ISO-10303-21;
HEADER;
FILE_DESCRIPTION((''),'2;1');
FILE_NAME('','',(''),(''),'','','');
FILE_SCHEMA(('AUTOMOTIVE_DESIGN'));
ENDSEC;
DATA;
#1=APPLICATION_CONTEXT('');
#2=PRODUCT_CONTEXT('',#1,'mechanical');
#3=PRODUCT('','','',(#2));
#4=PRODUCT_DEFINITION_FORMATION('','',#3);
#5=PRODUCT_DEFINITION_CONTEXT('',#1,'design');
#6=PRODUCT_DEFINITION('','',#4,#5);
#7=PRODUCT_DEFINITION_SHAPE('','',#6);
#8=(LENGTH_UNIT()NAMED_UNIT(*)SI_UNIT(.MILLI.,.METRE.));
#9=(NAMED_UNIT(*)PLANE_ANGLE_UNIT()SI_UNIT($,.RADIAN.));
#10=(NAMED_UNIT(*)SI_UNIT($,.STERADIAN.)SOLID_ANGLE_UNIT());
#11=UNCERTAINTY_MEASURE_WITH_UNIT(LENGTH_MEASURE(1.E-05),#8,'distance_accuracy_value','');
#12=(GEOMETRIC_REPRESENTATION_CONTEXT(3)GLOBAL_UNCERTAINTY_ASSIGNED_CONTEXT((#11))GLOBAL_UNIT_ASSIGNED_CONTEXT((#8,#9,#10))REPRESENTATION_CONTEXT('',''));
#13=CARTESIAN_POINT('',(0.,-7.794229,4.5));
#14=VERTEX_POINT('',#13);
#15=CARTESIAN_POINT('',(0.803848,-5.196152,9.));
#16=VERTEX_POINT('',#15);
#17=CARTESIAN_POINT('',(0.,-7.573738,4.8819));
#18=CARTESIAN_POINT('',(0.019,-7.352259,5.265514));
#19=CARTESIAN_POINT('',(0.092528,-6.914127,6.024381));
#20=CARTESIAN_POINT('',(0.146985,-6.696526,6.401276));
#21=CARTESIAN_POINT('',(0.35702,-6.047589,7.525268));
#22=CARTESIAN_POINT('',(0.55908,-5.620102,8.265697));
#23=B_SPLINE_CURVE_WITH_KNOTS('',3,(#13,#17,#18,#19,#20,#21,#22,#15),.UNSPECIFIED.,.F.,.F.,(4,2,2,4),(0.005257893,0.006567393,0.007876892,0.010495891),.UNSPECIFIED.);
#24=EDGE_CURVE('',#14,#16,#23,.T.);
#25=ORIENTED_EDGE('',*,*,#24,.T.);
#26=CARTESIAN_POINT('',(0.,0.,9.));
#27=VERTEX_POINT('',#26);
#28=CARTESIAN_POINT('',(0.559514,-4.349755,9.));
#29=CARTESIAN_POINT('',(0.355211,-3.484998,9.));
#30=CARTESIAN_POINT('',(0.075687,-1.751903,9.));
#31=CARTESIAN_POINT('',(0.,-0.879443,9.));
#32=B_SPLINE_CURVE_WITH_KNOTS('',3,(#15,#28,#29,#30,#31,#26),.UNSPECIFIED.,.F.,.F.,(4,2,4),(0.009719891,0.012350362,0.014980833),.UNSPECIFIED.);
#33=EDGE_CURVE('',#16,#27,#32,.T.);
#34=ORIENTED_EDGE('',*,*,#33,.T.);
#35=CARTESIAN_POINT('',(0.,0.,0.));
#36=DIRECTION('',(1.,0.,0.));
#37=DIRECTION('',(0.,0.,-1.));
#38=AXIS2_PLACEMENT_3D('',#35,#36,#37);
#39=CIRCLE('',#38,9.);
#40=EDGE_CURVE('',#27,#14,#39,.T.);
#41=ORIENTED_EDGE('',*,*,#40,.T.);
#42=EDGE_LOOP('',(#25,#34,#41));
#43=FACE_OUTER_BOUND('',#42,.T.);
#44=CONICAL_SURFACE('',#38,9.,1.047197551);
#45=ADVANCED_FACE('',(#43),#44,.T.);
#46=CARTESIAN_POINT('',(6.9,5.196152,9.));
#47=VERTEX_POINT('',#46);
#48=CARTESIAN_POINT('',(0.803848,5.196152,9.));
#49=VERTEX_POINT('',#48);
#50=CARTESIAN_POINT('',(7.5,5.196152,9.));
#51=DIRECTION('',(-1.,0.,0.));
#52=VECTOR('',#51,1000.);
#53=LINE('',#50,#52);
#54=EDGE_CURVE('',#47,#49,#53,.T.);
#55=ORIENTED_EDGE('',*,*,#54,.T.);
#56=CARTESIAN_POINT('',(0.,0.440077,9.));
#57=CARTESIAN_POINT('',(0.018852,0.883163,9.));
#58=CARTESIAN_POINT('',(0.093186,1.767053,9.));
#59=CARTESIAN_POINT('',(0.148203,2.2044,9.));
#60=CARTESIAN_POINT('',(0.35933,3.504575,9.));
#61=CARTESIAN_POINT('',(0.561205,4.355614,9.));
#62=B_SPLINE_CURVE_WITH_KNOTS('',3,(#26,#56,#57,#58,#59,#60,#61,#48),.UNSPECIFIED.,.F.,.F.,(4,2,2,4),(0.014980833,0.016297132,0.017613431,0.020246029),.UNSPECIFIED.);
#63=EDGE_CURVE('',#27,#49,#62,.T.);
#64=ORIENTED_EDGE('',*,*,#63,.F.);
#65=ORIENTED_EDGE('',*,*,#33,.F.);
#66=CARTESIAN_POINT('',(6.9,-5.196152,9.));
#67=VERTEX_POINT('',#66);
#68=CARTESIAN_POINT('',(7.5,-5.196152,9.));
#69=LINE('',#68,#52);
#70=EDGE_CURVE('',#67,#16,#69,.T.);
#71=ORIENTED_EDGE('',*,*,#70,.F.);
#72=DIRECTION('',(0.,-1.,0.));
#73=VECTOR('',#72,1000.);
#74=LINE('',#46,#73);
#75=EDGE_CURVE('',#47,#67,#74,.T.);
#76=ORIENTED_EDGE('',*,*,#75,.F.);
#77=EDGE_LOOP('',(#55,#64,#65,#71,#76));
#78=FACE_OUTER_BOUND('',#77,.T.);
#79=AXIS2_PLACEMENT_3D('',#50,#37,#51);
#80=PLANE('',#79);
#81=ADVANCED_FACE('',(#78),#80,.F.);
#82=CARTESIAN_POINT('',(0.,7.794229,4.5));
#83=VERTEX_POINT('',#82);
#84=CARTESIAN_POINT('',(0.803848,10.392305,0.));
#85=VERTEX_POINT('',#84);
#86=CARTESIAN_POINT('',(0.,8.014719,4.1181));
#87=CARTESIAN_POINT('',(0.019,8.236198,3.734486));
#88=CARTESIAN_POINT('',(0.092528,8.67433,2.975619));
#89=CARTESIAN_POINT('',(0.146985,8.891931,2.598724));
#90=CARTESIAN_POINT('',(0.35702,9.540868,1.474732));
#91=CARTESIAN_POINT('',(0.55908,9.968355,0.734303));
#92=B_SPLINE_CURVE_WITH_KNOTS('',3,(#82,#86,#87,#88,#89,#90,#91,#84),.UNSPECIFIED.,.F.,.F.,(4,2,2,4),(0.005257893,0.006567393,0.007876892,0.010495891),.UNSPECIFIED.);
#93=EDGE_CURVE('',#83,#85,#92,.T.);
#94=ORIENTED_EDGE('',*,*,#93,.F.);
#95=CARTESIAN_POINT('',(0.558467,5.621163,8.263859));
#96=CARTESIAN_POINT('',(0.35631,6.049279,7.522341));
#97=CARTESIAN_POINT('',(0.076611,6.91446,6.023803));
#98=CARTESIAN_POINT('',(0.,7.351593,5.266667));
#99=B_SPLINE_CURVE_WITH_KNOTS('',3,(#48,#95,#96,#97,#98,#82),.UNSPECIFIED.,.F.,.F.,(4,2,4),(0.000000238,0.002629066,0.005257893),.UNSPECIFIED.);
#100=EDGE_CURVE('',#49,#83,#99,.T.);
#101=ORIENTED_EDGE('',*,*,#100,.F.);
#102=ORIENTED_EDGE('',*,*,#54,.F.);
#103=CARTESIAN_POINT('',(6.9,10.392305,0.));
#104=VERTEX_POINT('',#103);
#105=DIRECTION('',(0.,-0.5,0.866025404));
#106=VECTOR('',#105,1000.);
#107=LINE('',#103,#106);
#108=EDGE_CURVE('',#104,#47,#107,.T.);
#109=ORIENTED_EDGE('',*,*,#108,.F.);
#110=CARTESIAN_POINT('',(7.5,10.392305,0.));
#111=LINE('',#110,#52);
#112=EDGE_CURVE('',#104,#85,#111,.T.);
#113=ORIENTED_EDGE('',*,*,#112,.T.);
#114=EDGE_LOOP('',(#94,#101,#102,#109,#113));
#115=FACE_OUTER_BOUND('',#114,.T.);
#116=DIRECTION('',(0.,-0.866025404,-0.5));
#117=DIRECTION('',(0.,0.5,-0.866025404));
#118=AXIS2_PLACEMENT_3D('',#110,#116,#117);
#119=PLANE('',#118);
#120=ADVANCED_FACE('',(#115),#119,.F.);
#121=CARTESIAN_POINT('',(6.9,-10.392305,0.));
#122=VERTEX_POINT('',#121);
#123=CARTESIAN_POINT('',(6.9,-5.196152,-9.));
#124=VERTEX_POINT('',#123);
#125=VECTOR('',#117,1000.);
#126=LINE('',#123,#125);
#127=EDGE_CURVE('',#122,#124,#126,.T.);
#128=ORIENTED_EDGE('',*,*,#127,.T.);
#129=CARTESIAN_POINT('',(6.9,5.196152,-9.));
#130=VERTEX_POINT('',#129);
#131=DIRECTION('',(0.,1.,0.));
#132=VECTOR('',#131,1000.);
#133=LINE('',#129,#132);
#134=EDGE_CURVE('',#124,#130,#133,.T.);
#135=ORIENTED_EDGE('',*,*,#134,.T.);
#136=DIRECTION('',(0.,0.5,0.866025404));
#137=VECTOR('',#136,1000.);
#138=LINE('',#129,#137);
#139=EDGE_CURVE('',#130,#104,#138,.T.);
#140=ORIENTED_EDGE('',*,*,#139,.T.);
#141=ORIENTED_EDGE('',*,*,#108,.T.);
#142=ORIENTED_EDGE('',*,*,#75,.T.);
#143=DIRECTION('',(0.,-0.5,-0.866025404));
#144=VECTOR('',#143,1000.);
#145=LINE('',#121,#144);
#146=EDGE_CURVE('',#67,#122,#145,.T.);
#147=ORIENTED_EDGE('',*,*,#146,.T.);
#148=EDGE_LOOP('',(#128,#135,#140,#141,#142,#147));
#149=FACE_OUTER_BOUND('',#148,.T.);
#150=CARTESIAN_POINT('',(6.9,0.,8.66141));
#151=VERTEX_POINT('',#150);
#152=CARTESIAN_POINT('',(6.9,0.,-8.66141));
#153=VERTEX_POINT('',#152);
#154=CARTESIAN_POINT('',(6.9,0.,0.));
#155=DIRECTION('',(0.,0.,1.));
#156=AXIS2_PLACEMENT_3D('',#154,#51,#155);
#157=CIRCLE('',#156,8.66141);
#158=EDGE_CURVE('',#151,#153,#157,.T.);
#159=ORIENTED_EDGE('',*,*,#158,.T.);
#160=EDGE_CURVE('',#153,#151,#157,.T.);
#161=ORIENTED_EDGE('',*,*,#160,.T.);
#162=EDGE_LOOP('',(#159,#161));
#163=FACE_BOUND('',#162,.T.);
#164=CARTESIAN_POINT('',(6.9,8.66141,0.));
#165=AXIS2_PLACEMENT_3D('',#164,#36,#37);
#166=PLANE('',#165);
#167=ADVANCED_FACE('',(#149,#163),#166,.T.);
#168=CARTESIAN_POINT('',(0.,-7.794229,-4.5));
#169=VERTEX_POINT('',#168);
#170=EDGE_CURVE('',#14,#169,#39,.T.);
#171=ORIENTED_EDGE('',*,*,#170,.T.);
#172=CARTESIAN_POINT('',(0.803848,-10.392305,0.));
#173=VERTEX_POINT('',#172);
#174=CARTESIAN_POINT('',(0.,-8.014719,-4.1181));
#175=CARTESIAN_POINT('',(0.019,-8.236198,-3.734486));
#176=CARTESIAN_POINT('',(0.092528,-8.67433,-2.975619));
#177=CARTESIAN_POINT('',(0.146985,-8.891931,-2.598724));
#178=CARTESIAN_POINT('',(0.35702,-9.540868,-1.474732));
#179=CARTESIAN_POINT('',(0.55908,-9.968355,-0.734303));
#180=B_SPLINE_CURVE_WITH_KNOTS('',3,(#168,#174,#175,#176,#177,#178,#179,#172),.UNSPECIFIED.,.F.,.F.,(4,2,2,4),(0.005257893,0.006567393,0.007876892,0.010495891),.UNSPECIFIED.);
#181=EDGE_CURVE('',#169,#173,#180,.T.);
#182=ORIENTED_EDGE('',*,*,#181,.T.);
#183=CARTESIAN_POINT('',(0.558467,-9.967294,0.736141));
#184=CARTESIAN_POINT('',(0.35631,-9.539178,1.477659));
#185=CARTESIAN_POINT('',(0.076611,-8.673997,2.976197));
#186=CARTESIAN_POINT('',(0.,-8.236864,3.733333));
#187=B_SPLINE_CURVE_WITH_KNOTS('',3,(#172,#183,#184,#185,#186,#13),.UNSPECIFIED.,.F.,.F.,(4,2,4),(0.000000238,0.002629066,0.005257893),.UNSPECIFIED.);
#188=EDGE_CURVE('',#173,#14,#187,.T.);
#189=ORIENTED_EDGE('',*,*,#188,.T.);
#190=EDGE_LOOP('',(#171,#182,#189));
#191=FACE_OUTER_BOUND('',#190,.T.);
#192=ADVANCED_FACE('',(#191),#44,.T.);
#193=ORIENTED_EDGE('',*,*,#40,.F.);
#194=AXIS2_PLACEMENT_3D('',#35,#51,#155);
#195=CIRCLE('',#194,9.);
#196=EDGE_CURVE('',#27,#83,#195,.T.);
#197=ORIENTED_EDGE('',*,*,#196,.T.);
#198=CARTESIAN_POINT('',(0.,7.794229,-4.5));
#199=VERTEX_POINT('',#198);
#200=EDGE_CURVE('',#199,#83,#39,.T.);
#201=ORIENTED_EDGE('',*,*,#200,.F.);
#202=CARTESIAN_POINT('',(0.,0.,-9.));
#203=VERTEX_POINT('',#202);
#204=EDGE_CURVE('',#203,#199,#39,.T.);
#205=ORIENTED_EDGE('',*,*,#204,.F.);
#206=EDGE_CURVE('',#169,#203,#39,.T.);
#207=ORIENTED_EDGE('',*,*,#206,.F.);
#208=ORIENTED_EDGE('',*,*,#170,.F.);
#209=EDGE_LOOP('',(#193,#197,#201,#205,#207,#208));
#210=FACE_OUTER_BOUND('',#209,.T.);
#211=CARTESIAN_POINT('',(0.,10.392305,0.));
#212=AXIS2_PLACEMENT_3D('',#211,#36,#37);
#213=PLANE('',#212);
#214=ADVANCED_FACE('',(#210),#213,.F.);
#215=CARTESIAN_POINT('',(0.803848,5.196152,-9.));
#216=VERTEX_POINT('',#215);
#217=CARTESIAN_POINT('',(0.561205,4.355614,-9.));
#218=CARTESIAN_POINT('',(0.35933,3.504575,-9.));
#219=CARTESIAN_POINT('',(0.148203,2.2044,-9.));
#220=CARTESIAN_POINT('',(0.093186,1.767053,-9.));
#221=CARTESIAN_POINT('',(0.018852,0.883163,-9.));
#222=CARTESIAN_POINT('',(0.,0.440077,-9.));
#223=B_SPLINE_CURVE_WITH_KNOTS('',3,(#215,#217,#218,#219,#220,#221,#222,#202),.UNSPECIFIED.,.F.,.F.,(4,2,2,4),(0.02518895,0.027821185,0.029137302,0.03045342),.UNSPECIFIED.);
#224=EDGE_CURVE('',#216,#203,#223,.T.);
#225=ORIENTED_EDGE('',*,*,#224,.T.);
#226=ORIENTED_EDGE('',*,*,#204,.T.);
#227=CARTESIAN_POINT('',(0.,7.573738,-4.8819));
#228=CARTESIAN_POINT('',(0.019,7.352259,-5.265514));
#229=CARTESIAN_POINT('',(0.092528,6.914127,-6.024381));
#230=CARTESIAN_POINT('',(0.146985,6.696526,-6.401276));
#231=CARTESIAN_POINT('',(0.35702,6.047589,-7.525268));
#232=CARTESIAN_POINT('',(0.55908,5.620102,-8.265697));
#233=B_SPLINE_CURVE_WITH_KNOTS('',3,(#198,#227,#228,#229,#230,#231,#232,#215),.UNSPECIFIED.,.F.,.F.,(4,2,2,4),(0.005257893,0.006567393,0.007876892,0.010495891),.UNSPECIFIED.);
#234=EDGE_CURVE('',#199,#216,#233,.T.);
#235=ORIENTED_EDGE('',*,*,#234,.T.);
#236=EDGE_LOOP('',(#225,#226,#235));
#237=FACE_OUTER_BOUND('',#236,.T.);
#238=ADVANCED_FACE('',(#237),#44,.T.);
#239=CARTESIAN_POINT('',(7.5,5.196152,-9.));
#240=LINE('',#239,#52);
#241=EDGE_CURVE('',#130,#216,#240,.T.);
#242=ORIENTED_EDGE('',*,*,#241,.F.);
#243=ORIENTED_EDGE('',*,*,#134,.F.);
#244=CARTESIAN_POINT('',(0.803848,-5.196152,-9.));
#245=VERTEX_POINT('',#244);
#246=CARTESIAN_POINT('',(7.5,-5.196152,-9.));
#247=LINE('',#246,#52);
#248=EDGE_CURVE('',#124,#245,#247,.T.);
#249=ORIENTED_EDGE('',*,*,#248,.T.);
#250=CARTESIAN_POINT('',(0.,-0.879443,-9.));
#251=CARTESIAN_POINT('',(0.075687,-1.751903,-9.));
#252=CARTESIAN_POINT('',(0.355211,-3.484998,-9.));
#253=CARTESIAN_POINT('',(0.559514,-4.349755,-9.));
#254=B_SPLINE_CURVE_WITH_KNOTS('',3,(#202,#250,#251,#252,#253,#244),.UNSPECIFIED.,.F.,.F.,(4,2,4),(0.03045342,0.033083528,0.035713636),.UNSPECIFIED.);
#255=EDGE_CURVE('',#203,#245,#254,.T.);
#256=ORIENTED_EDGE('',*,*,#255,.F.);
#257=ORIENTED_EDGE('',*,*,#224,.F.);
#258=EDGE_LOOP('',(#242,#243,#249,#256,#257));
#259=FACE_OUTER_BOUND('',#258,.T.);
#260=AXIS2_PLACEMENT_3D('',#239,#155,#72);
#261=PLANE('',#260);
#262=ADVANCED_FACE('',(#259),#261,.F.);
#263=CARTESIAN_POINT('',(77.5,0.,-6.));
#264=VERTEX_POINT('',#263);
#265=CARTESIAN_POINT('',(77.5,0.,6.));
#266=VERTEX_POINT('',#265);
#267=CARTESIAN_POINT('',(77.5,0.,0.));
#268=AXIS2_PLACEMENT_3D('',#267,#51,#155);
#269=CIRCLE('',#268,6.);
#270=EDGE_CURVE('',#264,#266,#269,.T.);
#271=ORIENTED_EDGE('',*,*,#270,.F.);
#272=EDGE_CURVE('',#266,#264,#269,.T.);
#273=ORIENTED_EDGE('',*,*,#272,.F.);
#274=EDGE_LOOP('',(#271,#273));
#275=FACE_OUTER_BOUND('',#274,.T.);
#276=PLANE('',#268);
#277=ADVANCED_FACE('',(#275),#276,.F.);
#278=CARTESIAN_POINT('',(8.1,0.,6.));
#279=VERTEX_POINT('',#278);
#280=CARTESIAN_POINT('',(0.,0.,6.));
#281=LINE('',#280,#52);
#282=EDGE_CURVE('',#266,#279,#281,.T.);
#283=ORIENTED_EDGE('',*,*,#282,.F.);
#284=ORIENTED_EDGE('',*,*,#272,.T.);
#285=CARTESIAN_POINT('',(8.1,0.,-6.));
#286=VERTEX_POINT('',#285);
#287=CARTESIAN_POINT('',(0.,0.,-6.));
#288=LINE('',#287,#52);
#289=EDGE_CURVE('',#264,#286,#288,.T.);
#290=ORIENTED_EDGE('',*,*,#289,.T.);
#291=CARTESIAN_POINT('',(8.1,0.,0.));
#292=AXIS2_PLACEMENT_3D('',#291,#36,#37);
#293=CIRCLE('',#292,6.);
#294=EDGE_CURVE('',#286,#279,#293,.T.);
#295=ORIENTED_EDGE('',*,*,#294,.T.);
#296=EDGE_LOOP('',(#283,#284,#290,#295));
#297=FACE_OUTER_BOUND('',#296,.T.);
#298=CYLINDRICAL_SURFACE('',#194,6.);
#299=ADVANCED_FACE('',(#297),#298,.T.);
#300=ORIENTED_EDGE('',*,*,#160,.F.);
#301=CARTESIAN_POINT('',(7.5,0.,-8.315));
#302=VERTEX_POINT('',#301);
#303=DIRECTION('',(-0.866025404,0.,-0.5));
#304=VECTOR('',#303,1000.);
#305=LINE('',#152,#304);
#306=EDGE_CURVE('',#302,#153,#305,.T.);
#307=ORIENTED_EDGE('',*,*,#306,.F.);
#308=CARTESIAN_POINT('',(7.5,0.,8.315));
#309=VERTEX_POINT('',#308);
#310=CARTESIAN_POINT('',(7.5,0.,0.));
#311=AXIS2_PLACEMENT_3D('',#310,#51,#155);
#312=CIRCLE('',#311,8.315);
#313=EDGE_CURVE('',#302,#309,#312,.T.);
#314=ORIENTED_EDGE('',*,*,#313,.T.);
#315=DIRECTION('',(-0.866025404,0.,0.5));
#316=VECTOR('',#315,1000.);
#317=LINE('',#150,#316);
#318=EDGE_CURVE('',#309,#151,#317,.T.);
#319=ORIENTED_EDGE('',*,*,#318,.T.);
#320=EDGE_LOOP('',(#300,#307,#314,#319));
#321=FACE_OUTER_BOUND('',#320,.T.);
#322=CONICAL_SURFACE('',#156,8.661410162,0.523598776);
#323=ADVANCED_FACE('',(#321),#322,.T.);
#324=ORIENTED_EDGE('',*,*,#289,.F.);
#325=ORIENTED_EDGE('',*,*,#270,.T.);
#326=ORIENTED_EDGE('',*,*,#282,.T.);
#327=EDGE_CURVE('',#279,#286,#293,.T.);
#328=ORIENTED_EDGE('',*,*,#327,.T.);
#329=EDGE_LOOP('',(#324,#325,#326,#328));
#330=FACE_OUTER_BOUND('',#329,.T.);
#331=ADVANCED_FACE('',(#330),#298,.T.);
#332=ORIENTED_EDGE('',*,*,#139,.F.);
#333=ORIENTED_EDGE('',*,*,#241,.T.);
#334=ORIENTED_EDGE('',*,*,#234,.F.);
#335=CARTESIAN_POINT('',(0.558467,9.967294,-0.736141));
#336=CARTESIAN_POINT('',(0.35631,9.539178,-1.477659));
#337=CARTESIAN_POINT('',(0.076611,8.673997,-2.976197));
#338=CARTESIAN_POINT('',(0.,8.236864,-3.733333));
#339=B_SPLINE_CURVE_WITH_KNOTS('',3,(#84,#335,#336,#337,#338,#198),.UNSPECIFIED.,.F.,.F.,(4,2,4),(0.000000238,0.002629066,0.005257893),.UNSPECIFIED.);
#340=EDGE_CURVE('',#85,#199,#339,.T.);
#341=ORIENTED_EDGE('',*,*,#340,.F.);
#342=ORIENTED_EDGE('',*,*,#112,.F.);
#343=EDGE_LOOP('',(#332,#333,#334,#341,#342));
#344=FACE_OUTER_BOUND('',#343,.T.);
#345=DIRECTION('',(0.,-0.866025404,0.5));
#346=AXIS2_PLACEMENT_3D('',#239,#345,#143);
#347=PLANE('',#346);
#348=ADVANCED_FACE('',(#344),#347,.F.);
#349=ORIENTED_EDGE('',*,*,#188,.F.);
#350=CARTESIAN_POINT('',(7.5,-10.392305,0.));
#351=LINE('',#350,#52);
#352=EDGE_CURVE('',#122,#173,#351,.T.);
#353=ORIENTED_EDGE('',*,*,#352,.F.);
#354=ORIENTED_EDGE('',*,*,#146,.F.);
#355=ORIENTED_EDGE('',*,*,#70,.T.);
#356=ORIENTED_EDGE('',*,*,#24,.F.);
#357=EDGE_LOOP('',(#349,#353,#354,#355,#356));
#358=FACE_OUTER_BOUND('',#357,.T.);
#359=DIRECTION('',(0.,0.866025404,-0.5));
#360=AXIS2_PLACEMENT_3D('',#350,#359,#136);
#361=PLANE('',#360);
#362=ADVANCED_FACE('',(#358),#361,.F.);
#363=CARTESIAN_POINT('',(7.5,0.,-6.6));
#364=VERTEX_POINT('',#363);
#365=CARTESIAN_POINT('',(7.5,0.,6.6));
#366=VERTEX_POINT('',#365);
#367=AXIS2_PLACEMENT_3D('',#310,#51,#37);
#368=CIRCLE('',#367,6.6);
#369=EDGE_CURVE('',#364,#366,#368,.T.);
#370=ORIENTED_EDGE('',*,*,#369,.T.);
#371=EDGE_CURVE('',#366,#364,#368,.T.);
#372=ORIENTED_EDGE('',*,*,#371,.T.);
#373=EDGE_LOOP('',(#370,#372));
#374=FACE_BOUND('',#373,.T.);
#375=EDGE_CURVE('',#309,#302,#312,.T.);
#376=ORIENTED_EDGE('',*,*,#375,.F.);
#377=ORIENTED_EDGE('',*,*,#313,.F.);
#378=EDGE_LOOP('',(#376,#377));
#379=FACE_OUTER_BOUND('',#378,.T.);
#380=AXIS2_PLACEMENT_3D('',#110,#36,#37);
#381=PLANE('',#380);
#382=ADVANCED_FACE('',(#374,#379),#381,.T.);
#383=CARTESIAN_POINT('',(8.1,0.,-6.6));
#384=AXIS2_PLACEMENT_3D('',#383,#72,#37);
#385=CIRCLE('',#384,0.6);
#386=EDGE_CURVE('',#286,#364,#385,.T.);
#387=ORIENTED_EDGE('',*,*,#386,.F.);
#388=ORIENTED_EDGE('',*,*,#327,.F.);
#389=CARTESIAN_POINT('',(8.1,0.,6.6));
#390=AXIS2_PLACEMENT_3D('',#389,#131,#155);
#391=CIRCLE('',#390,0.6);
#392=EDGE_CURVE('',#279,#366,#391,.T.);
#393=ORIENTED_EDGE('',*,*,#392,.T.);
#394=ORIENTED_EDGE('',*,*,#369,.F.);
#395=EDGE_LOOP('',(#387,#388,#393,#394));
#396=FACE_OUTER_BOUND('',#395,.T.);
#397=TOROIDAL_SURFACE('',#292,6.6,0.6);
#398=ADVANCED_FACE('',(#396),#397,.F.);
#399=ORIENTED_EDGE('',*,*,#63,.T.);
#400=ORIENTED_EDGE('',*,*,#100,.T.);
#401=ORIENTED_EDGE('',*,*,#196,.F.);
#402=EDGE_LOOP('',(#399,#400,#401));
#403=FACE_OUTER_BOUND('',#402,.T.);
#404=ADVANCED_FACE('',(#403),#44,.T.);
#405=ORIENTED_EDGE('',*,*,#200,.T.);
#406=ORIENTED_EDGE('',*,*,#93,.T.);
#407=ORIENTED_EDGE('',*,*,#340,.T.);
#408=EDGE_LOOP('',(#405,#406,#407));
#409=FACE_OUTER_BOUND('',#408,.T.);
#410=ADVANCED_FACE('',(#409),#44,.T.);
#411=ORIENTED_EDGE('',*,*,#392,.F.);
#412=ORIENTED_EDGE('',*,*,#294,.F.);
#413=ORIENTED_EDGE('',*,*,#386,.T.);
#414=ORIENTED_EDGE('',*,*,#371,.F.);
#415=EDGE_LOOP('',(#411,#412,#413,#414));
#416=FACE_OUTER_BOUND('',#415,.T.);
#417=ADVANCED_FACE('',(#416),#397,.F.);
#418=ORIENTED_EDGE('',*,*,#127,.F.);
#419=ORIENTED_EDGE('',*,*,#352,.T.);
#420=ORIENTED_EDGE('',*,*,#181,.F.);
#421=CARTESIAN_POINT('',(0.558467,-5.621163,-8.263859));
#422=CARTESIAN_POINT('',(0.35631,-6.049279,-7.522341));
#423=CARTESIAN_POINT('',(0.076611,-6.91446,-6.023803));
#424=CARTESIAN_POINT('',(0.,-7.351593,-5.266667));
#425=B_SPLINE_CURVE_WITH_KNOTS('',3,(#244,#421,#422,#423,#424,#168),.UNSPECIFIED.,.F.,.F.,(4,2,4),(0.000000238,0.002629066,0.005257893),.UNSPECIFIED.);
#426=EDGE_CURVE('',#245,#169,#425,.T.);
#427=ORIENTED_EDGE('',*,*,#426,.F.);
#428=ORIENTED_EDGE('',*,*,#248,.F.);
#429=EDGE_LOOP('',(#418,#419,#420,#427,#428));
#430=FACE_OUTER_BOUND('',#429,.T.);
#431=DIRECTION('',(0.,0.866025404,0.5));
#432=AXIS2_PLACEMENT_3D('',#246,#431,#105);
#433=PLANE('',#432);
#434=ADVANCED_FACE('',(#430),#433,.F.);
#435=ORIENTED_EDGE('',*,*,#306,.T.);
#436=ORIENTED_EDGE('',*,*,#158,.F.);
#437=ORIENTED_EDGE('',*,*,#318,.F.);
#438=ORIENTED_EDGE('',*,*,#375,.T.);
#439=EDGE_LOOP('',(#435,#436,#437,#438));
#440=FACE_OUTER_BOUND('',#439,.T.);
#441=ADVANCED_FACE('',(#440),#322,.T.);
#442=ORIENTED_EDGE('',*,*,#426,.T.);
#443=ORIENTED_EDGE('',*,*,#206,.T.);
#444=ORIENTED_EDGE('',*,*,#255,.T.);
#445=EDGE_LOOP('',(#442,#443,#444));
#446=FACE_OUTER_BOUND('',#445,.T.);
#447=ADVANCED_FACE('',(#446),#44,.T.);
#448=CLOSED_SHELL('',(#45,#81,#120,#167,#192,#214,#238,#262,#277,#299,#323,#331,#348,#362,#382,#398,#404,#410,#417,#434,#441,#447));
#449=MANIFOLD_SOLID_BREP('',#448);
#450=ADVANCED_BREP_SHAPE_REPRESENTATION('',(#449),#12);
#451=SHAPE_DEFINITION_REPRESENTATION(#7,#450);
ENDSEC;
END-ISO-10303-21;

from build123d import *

# Parameters (mm, degrees)
BASE_EXTRUDE_DEPTH = 7.5
FILLET_2_R         = 0.6


with BuildPart() as part:
    # Sketch1 → Base-Extrude (new body)
    with BuildSketch(Plane(origin=(0, 0, 0), x_dir=(0, 0, -1), z_dir=(1, 0, 0))):
        Polygon((9, 5.196152423), (9, -5.196152423), (0, -10.392304845), (-9, -5.196152423), (-9, 5.196152423), (0, 10.392304845), align=None)
    extrude(amount=BASE_EXTRUDE_DEPTH)

    # Sketch2 → Boss-Revolve1 (revolve)
    with BuildSketch(Plane.XY, mode=Mode.PRIVATE) as boss_revolve1_sk:
        Polygon((0, 0), (77.5, 0), (77.5, 4.4845), (77.5, 6), (47.5, 6), (0, 6), align=None)
    revolve(boss_revolve1_sk.sketch.rotate(Axis((0, 0, 0), (1, 0, 0)), 90), axis=Axis((0, 0, 0), (1, 0, 0)))

    # Sketch3 → Cut-Revolve1 (revolve, cut)
    with BuildSketch(Plane.XY):
        Polygon((0, 9), (3.690598923, 15.392304845), (3.690598923, 20.392304845), (-10, 20.392304845), (-10, 9), align=None)
    revolve(axis=Axis((0, 0, 0), (1, 0, 0)), mode=Mode.SUBTRACT)

    # Sketch4 → Cut-Revolve3 (revolve, cut)
    with BuildSketch(Plane.XY, mode=Mode.PRIVATE) as cut_revolve3_sk:
        Polygon((7.5, 8.315), (6.9, 8.661410162), (6.9, 10.392304845), (7.5, 10.392304845), align=None)
    revolve(cut_revolve3_sk.sketch.rotate(Axis((0, 0, 0), (1, 0, 0)), 90), axis=Axis((0, 0, 0), (1, 0, 0)), mode=Mode.SUBTRACT)

    # Fillet 2
    fillet_2_edges = [part.edges().sort_by_distance(p)[0] for p in [
        (7.5, 0, -6),
    ]]
    fillet(fillet_2_edges, radius=FILLET_2_R)


solid = part.part
